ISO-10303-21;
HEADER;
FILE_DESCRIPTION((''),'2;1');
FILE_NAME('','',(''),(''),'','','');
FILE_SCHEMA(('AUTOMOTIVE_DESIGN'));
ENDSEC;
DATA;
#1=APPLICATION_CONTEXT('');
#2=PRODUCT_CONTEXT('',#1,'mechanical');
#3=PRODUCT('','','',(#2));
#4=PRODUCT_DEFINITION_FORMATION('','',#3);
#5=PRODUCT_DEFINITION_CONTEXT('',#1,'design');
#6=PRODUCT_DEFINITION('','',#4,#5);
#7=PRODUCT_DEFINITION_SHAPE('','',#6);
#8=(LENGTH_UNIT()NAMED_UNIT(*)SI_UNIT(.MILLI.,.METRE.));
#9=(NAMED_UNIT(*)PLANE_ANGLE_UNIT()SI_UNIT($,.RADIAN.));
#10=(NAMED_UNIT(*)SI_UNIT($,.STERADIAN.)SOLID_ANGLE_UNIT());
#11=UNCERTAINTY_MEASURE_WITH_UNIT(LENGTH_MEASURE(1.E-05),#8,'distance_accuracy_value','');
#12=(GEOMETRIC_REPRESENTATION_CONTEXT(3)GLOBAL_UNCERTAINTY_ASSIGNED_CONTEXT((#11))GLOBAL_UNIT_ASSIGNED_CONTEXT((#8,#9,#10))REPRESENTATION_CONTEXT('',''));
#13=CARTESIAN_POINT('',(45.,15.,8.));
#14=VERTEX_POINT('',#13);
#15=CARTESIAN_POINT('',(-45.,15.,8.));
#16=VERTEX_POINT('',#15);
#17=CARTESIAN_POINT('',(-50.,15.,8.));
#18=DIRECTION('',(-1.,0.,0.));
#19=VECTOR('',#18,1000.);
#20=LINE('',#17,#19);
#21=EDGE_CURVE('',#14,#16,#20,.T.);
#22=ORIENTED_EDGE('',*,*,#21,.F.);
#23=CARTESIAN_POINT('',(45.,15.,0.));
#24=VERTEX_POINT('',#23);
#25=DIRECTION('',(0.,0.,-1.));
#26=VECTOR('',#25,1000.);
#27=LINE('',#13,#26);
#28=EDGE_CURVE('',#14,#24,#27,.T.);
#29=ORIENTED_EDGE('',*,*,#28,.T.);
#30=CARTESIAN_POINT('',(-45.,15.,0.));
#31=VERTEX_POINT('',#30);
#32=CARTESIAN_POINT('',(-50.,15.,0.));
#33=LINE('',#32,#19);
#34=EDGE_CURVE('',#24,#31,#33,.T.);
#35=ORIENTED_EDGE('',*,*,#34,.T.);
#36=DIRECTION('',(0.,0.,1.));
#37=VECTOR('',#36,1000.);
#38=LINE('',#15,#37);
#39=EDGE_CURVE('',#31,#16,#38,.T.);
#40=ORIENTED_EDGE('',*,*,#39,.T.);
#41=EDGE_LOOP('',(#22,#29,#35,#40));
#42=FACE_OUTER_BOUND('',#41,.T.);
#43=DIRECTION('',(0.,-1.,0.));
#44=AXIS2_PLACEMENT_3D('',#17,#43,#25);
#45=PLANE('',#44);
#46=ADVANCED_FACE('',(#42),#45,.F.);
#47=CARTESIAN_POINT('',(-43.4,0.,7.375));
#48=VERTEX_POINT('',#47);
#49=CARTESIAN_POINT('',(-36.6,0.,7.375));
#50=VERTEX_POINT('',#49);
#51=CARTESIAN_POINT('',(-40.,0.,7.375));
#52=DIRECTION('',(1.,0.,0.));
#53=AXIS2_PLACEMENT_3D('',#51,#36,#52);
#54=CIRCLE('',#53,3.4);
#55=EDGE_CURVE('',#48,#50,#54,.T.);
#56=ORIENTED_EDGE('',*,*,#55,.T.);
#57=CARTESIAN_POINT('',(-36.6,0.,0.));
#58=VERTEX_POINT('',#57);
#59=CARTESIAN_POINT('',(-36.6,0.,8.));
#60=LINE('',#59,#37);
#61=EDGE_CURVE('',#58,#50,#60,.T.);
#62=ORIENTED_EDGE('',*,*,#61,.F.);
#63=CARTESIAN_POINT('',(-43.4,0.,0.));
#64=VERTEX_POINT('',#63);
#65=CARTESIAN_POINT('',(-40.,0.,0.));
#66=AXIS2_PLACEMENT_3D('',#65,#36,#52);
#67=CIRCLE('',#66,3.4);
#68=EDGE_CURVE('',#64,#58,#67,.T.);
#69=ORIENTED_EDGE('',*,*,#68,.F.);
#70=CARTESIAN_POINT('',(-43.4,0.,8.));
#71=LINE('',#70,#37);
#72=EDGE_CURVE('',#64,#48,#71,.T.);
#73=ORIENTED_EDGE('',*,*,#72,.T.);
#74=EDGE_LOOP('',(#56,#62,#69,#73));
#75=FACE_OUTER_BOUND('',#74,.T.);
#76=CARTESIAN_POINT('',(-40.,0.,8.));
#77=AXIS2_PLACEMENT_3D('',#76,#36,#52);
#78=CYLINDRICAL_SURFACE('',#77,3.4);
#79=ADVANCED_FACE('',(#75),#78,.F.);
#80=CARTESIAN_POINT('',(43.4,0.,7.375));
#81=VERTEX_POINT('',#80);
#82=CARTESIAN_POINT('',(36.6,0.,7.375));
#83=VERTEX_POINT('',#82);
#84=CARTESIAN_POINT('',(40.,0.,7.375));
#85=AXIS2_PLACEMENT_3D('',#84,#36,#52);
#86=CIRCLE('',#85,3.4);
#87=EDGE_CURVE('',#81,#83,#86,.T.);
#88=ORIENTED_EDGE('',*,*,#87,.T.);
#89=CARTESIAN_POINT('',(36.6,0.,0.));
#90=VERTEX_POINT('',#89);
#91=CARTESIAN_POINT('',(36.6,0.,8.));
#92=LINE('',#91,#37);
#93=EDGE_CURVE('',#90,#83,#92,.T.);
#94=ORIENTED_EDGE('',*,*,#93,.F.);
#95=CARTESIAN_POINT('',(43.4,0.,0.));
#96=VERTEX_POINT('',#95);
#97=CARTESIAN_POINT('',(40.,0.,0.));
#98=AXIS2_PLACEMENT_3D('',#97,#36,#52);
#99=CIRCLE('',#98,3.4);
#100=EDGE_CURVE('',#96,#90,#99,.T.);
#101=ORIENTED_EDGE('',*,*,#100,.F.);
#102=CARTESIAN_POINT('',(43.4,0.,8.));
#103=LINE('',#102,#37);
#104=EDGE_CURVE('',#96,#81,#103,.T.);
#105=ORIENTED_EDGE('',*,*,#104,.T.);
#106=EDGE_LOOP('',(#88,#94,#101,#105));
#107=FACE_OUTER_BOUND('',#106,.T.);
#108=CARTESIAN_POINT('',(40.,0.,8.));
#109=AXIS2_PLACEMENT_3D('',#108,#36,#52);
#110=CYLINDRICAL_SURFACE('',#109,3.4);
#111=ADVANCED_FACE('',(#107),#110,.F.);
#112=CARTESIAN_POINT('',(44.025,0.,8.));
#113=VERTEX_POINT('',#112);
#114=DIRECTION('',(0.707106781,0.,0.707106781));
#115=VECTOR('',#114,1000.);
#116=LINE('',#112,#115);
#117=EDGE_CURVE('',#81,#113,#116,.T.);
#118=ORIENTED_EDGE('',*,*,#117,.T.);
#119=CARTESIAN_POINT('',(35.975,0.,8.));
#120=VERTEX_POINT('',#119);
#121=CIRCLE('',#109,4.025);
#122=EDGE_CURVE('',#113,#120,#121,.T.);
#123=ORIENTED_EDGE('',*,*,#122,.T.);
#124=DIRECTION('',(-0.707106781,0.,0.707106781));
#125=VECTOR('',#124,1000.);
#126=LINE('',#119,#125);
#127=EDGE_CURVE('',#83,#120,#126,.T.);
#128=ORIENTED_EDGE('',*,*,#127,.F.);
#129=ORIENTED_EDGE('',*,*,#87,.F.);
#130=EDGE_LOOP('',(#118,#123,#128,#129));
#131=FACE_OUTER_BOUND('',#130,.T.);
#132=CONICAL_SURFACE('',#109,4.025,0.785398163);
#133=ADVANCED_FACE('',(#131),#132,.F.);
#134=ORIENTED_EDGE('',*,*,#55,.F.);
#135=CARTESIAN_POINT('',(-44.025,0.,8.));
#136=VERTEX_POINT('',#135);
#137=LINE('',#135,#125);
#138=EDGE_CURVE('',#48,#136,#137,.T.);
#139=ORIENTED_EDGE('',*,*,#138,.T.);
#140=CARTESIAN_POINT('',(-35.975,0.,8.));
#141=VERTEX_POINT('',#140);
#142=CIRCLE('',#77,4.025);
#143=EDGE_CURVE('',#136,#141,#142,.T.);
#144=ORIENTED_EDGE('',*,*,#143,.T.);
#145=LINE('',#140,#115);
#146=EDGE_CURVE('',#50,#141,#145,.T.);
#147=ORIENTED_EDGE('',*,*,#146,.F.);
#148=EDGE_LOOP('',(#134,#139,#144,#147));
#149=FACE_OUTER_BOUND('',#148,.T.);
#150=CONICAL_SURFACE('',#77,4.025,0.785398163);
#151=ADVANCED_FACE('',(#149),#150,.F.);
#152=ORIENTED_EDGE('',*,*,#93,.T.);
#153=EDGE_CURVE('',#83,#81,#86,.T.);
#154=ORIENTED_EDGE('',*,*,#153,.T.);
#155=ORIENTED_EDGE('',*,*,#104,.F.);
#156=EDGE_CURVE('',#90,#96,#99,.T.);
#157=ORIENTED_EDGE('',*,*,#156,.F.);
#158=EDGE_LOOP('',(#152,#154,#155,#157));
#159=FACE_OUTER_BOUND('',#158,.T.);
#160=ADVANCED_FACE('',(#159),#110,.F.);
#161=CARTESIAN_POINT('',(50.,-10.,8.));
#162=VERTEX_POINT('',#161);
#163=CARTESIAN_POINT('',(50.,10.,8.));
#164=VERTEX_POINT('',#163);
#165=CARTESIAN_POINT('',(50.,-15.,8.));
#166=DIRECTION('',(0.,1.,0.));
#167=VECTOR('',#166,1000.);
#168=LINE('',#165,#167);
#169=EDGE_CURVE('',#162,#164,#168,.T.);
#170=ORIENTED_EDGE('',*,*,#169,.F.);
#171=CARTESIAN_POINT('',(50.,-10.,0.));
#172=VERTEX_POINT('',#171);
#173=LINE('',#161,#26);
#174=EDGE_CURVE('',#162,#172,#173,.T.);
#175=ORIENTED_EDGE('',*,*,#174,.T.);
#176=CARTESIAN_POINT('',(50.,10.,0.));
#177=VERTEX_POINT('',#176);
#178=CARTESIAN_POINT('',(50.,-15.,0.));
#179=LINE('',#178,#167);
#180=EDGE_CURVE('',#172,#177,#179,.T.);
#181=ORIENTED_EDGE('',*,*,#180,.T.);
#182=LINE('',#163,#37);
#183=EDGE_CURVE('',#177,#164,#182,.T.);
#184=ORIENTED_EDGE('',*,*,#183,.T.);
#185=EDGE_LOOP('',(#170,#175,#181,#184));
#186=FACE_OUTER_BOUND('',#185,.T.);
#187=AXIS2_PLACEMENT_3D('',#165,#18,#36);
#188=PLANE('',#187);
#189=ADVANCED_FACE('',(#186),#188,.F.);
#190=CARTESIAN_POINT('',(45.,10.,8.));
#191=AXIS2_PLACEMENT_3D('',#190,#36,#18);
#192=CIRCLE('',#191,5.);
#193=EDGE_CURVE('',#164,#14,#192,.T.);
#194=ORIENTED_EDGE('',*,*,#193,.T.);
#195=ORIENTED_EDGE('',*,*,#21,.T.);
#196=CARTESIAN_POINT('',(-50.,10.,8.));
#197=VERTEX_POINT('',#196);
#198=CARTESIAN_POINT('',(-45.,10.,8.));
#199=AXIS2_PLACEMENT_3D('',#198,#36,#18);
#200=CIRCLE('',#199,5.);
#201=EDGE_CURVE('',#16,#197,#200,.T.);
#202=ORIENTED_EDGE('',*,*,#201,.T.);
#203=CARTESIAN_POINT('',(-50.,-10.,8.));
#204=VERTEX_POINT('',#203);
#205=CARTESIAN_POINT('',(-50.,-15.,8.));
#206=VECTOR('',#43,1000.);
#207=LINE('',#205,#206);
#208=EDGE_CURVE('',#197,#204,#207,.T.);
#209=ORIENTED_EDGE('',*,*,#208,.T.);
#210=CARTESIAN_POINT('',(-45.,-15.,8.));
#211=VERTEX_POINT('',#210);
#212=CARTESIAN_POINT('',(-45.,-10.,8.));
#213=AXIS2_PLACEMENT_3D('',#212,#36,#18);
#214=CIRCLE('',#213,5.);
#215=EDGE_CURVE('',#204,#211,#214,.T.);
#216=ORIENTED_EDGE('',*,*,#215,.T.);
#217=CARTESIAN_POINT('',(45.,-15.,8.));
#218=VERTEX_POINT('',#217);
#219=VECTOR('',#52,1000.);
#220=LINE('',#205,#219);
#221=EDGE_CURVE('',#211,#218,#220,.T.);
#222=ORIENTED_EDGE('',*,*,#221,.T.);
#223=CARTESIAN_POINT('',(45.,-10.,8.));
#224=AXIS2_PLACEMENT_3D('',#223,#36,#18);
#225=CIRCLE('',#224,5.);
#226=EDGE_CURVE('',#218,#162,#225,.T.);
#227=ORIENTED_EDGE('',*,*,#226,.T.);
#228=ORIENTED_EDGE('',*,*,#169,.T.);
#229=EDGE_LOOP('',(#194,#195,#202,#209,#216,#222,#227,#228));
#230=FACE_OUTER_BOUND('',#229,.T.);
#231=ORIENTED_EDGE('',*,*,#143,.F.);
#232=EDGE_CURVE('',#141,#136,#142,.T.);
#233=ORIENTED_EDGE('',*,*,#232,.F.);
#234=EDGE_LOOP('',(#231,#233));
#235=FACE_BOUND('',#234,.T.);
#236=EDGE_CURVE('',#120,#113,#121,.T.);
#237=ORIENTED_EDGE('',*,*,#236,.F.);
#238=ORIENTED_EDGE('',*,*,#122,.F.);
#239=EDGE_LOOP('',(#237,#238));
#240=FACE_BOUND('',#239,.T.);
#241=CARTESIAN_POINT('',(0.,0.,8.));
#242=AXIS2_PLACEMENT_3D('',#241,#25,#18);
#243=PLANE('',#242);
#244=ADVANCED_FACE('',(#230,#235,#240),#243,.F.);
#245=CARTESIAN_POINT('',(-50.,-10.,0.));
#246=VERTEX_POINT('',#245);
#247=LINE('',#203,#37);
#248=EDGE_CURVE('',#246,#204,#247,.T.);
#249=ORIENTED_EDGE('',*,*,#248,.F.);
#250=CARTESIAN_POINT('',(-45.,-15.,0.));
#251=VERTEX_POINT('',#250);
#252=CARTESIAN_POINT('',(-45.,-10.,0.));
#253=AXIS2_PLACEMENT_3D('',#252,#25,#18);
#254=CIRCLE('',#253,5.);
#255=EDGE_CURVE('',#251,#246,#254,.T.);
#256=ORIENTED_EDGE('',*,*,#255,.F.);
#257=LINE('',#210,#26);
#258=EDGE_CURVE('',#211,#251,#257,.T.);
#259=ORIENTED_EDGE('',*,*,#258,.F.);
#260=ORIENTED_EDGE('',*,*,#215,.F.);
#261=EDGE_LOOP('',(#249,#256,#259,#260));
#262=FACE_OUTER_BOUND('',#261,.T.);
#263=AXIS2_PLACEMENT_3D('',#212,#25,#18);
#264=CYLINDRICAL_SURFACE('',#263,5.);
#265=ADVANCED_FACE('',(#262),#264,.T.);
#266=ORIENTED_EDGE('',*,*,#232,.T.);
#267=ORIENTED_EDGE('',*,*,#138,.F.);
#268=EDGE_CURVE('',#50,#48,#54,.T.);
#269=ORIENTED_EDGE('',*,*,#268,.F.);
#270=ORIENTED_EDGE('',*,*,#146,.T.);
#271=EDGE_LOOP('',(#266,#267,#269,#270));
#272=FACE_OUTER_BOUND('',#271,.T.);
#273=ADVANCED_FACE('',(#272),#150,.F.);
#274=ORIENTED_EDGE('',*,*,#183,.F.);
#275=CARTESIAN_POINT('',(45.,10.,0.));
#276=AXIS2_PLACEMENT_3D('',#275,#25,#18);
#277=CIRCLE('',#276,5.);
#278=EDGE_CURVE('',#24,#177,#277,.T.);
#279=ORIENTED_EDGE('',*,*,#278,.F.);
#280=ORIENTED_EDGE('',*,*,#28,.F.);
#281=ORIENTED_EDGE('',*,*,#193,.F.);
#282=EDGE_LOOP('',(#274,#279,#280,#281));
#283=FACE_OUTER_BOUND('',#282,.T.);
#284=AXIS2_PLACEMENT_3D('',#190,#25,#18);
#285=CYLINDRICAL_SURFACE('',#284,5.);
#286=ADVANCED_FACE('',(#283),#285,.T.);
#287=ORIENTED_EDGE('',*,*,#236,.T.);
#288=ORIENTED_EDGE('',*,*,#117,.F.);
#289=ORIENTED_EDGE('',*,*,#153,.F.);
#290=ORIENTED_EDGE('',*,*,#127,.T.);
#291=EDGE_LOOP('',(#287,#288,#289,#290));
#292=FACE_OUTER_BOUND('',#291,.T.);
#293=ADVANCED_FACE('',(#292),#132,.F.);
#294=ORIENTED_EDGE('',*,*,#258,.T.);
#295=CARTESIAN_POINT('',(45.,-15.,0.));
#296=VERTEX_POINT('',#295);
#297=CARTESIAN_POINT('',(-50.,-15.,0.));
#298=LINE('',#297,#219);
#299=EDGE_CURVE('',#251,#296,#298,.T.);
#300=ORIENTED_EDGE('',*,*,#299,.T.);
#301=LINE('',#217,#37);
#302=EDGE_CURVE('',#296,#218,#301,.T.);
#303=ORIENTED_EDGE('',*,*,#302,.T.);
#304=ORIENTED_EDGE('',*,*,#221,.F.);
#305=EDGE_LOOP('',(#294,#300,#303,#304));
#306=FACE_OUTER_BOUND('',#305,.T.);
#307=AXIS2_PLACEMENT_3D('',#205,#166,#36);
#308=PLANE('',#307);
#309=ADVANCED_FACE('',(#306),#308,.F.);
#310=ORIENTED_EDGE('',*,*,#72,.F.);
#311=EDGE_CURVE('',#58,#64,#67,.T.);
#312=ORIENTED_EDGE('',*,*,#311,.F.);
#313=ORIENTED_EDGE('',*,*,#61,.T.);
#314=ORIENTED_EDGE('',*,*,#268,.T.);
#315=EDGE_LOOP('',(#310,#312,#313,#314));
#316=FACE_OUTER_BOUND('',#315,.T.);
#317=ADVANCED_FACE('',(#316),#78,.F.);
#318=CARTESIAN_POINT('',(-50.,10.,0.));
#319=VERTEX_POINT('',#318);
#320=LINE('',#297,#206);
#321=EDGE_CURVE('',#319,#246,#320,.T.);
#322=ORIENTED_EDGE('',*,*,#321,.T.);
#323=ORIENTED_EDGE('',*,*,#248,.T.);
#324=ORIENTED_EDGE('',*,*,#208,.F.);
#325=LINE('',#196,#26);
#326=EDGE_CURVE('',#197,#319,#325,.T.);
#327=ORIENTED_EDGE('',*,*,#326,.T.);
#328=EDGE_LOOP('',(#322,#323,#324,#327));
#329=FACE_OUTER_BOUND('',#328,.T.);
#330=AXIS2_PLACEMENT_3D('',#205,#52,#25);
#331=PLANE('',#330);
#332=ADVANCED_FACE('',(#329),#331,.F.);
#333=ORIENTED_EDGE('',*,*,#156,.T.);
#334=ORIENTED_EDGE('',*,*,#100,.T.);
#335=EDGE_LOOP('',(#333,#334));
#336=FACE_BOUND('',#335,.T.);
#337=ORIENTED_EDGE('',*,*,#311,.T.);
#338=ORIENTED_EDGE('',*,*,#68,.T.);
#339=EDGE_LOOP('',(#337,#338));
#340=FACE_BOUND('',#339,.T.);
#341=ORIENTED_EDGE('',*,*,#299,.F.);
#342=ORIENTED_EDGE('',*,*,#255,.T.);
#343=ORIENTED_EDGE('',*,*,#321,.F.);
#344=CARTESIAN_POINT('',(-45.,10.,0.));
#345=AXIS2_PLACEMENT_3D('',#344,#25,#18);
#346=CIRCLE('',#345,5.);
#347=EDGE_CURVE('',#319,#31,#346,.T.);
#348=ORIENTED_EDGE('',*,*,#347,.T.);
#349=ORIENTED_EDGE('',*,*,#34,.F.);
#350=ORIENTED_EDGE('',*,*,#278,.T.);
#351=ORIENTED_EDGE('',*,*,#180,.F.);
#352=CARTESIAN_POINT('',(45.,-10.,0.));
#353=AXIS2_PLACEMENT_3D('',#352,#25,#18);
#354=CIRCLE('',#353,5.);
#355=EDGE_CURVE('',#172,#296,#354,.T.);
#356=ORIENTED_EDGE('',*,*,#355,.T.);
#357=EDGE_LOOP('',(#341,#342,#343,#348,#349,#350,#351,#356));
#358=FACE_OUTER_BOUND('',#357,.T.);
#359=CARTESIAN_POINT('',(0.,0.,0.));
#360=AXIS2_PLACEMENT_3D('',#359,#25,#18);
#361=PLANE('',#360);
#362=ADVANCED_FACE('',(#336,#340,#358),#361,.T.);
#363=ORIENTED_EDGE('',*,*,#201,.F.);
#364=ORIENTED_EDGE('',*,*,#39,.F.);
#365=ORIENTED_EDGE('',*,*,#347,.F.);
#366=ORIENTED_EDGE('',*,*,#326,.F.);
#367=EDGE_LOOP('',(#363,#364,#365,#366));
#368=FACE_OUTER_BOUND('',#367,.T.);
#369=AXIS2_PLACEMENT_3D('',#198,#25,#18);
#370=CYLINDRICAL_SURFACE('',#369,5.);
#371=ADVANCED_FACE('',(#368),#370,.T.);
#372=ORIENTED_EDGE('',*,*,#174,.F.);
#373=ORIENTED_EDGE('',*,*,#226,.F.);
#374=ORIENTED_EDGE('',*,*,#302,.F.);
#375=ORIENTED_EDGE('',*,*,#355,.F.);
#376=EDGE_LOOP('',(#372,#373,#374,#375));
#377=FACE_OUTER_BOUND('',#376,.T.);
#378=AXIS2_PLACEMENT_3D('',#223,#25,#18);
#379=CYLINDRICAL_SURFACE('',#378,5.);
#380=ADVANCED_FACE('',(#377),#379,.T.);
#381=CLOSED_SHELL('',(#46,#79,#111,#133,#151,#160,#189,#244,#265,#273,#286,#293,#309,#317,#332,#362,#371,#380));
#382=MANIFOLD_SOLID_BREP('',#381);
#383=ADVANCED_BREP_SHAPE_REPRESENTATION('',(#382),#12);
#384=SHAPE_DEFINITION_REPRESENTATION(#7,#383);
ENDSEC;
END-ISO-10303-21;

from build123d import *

# Parameters (mm, degrees)
SKETCH1_W                   = 100
SKETCH1_H                   = 30
BOSS_EXTRUDE1_DEPTH         = 8
FILLET1_R                   = 5
M8_TAPPED_HOLE1_D           = 6.8
M8_TAPPED_HOLE1_CSINK_D     = 8.05
M8_TAPPED_HOLE1_CSINK_ANGLE = 90


with BuildPart() as part:
    # Sketch1 → Boss-Extrude1 (new body)
    with BuildSketch(Plane.XY):
        Rectangle(SKETCH1_W, SKETCH1_H)
    extrude(amount=BOSS_EXTRUDE1_DEPTH)

    # Fillet1
    fillet1_edges = [part.edges().sort_by_distance(p)[0] for p in [
        (50, -15, 4),
        (-50, -15, 4),
        (-50, 15, 4),
        (50, 15, 4),
    ]]
    fillet(fillet1_edges, radius=FILLET1_R)

    # M8 Tapped Hole1 (through all)
    with Locations(Plane.XY.offset(8)):
        with Locations((-40, 0), (40, 0)):
            CounterSinkHole(M8_TAPPED_HOLE1_D / 2, M8_TAPPED_HOLE1_CSINK_D / 2, counter_sink_angle=M8_TAPPED_HOLE1_CSINK_ANGLE)


solid = part.part
